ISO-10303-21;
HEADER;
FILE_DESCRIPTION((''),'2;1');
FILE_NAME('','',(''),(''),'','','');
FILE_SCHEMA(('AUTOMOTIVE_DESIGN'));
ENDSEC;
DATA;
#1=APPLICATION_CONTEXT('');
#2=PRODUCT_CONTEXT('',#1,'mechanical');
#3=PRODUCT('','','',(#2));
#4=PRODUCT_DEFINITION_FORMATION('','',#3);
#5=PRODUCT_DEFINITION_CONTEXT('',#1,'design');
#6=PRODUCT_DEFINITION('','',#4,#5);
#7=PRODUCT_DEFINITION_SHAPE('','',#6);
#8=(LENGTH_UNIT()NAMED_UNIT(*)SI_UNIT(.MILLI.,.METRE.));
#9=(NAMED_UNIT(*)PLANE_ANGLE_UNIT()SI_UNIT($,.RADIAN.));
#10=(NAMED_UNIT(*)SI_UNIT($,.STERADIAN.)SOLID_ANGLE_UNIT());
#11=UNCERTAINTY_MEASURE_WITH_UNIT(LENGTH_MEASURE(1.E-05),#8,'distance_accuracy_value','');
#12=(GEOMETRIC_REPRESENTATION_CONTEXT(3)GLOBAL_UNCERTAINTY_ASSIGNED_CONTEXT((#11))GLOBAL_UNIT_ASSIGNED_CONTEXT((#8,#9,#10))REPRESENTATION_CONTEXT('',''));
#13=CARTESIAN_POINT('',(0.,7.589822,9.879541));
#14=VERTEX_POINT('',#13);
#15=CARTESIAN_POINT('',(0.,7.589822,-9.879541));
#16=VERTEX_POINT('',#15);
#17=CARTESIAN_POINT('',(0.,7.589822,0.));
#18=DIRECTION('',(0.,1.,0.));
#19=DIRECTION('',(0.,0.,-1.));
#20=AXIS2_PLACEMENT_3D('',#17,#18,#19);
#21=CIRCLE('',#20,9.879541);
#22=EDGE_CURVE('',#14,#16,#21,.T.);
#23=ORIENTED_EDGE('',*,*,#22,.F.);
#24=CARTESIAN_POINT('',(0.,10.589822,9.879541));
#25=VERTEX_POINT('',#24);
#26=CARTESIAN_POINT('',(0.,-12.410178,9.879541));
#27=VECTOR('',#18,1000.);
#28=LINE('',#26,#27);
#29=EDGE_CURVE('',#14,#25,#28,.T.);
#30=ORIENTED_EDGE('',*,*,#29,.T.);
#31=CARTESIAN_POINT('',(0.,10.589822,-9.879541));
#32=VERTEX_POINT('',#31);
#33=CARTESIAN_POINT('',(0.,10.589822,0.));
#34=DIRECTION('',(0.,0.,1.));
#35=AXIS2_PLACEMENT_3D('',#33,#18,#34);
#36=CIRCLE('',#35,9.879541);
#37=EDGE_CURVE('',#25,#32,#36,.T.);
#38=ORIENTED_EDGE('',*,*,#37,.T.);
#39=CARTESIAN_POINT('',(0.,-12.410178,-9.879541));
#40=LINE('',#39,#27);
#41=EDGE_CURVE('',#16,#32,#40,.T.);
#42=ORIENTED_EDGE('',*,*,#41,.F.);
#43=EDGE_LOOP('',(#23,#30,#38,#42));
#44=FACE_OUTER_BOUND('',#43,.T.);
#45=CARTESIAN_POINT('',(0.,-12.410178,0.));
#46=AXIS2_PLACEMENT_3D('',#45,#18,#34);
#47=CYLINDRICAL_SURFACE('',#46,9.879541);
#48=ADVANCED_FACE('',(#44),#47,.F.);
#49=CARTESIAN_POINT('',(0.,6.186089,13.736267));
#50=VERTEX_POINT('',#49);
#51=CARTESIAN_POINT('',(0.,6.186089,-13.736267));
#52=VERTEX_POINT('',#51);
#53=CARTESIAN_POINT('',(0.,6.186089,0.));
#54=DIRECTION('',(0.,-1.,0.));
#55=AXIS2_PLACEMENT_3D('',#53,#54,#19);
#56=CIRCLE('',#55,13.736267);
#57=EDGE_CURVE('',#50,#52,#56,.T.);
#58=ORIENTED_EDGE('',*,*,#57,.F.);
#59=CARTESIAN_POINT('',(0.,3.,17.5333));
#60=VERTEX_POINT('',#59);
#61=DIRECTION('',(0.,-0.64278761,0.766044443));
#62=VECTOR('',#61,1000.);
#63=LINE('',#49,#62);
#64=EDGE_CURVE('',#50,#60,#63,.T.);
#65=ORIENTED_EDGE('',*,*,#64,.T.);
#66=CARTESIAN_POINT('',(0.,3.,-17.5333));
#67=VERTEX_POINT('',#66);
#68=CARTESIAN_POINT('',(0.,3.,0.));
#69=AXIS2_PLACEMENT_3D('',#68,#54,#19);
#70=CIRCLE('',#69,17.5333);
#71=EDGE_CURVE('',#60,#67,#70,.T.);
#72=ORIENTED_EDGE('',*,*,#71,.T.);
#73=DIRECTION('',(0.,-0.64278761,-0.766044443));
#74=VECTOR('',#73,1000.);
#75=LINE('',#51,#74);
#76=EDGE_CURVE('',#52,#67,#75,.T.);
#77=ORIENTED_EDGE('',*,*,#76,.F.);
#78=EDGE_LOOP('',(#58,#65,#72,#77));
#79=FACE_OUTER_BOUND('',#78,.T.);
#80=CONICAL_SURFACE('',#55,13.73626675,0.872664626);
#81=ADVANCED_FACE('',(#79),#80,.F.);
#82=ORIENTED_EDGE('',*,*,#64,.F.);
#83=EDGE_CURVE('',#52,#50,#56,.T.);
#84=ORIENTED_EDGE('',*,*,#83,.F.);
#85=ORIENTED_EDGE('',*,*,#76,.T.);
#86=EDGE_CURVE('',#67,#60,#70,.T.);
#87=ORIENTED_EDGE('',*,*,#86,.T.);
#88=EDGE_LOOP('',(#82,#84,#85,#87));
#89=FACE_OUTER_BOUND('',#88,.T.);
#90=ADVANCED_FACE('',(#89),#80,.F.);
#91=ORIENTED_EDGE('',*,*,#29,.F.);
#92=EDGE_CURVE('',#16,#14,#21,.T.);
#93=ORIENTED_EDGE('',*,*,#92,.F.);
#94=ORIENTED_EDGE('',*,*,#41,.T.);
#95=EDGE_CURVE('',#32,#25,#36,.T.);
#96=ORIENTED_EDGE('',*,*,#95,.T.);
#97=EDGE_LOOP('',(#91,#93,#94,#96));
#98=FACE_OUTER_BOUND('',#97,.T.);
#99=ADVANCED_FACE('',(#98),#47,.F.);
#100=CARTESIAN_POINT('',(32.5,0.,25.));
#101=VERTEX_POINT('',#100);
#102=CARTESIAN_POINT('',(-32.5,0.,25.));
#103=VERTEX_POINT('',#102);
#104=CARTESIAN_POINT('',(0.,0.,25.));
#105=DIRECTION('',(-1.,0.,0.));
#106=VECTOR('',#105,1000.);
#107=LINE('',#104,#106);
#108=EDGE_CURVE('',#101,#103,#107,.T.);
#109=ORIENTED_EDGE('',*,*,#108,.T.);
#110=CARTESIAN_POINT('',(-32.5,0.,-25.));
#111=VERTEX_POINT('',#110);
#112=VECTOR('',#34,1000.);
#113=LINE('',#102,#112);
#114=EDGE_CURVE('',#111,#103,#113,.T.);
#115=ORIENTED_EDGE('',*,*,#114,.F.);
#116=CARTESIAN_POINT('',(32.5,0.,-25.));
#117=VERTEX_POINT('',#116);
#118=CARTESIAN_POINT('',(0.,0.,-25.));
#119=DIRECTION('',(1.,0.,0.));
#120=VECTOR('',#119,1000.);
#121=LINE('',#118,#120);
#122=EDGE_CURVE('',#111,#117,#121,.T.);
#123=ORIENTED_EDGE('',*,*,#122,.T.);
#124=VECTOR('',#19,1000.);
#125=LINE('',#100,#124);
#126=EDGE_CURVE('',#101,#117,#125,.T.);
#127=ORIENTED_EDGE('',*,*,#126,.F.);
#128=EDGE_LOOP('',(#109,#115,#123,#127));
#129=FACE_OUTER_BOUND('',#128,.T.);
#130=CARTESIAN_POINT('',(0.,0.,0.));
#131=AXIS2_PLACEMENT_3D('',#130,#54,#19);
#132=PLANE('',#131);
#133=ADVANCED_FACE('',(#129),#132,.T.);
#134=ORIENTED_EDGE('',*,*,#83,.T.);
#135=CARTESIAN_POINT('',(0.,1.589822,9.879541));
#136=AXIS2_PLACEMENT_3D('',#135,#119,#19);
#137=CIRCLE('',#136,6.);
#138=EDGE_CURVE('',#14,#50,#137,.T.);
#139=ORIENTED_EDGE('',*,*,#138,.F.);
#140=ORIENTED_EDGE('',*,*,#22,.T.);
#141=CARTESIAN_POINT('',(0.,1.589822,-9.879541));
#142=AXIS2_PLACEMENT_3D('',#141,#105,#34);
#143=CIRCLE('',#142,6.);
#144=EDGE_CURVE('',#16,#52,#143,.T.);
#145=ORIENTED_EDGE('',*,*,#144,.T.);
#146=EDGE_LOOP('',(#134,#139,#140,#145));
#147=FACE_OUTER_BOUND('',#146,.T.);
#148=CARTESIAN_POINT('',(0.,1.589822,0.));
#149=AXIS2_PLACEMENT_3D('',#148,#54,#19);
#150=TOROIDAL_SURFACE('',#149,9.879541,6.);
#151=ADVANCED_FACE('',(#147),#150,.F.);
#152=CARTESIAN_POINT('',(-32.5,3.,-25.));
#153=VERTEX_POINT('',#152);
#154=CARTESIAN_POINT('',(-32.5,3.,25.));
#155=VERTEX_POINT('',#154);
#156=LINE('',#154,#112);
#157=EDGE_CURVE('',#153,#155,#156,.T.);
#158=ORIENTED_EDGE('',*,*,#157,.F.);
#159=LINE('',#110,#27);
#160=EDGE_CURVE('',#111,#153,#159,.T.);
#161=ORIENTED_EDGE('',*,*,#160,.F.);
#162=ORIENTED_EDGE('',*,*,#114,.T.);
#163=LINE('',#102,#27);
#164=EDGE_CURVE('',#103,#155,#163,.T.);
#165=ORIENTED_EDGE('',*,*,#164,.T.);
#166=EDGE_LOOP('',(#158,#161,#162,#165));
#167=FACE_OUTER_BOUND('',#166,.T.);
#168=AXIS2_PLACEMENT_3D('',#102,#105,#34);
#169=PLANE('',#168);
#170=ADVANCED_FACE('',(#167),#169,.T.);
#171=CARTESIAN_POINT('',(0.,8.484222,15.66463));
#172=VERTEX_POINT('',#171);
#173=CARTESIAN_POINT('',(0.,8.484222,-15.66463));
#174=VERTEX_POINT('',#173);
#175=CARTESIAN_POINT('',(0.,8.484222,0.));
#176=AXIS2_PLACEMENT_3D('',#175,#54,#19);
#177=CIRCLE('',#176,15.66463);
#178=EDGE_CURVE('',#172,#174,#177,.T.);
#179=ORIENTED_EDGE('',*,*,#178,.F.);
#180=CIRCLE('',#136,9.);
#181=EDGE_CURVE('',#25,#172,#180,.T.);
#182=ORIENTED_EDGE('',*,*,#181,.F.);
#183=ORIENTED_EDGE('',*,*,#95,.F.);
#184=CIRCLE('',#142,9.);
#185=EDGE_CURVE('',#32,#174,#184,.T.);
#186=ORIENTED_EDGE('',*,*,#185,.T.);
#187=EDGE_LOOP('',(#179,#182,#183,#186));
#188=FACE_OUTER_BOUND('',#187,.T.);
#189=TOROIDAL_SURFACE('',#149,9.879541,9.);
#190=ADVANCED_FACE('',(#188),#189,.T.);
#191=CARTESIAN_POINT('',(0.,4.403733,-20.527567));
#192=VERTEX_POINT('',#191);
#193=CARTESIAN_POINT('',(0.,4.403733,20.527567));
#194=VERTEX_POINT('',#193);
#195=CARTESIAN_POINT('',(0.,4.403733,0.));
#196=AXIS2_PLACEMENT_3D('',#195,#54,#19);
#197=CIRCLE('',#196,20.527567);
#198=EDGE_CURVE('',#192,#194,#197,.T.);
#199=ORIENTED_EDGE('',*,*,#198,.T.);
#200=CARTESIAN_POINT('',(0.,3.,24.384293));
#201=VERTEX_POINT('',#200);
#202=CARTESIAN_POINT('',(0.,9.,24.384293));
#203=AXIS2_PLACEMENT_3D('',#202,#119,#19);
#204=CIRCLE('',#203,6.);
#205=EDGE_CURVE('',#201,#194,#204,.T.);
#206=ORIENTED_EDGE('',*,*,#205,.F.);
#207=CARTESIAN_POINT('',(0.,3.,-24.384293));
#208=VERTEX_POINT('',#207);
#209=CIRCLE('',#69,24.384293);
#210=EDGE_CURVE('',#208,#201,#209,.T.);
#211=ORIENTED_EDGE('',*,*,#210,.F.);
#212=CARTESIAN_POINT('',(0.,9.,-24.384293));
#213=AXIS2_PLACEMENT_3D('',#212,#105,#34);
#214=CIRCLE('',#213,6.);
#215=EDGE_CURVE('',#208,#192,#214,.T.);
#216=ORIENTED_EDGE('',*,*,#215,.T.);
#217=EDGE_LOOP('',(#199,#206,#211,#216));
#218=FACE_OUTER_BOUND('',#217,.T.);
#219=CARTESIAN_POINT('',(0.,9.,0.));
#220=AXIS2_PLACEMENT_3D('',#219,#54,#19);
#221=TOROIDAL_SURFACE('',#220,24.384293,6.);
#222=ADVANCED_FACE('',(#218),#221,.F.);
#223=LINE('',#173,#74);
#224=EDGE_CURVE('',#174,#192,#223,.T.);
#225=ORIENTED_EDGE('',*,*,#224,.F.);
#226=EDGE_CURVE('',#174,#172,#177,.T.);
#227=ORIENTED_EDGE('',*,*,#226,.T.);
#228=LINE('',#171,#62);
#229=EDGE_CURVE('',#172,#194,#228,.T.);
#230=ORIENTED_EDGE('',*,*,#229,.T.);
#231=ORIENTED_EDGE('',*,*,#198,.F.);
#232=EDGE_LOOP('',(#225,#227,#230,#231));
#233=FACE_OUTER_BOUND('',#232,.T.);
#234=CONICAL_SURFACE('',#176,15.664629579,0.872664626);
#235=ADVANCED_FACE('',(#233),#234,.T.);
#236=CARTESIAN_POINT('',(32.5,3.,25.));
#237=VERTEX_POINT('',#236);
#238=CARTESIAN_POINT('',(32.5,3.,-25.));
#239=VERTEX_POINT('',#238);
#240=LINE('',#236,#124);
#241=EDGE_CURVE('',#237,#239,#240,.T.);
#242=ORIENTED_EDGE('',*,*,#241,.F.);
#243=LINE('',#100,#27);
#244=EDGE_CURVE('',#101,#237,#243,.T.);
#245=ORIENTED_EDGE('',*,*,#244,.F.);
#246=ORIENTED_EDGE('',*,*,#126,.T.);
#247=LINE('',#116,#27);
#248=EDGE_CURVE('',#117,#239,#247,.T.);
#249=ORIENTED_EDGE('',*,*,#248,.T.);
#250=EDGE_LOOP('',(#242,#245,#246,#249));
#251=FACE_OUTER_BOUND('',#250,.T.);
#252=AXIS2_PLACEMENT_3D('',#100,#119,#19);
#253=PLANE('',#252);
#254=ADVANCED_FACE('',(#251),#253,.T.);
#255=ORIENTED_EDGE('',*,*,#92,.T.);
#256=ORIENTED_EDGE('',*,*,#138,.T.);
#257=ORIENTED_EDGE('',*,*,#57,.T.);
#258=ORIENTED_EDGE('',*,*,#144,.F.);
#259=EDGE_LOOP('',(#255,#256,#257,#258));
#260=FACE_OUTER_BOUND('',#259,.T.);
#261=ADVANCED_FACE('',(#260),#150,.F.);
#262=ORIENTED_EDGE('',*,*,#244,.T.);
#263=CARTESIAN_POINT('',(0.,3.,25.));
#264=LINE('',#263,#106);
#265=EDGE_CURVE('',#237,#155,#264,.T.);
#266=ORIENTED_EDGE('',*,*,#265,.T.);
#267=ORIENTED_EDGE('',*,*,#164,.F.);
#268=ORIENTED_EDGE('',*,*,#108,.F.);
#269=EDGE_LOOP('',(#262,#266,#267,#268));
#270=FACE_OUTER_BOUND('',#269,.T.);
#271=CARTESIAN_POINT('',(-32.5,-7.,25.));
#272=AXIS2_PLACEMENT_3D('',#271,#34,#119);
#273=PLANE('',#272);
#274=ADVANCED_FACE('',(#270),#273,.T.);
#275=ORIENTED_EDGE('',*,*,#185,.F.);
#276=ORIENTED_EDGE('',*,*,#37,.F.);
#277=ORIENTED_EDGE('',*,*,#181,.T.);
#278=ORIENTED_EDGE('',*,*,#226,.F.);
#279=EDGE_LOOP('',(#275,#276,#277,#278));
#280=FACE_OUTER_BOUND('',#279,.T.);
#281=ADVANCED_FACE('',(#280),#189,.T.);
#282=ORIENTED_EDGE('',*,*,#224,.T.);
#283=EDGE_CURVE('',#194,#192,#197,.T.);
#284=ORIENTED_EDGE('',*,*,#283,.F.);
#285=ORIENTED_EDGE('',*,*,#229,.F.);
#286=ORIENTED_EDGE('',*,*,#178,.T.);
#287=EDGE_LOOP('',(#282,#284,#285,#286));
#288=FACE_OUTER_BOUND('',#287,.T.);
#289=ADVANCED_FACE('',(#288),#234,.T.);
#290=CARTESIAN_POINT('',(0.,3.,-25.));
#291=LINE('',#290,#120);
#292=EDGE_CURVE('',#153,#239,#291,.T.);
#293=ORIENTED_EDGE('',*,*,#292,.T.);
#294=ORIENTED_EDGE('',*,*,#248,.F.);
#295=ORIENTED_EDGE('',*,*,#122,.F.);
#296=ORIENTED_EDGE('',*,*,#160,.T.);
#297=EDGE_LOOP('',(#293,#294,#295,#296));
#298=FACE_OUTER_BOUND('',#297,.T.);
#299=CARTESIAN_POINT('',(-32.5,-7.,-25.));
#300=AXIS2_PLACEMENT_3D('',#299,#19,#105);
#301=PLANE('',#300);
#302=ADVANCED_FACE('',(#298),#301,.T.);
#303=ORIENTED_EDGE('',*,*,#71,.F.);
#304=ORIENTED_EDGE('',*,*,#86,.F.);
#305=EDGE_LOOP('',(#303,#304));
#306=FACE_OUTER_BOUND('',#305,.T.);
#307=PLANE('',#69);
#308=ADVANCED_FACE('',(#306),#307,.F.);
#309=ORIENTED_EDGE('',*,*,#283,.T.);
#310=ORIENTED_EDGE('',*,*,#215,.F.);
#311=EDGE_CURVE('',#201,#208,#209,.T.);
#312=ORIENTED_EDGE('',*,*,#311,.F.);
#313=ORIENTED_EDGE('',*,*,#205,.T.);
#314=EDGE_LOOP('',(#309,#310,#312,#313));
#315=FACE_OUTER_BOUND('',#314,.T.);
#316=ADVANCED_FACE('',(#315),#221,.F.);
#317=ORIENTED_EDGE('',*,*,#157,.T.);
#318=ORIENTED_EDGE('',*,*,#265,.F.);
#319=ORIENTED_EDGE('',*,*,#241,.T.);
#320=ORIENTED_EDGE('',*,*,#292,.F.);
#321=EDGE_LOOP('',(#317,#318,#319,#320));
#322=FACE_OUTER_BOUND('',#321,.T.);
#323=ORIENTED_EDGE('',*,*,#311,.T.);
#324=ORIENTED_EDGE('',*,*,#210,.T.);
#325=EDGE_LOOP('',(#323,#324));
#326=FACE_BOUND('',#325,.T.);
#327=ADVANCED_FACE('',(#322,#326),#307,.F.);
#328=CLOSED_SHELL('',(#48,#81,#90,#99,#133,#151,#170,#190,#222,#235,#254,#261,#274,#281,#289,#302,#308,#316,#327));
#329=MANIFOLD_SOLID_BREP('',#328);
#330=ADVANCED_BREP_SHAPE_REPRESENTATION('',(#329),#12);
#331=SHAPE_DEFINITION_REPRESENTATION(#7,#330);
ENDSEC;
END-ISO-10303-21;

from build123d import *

# Parameters (mm, degrees)
HUB_PROFILE_SKETCH_W                   = 7
HUB_PROFILE_SKETCH_H                   = 3
PLATE_OUTLINE_SKETCH_65X50_OUTSIDE_W   = 85.506
PLATE_OUTLINE_SKETCH_65X50_OUTSIDE_H   = 85.506
PLATE_OUTLINE_SKETCH_65X50_OUTSIDE_W_2 = 65
PLATE_OUTLINE_SKETCH_65X50_OUTSIDE_H_2 = 50
HUB_TRIM_CUT_65X50_DEPTH               = 10
BASE_PLATE_SKETCH_65X50_W              = 65
BASE_PLATE_SKETCH_65X50_H              = 50
BASE_PLATE_65X50X3_DEPTH               = 3
PLATE_CORNER_FILLETS_R6_R              = 6
MOUNTING_HOLES_SKETCH_R                = 2.5
MOUNTING_HOLES_4X_DEPTH                = 3
MOUNTING_HOLE_CHAMFERS_1_5X45_SIZE     = 1.5
CENTER_BORE_SKETCH_R                   = 9.879541092
CENTER_BORE_CUT_DEPTH                  = 23
HUB_GROOVE_SKETCH_45_R                 = 22.5
HUB_GROOVE_45_DEPTH                    = 3
SKETCH3_2_W                            = 65
SKETCH3_2_H                            = 50
PLATE_STEP_65X50X3_DEPTH               = 3


with BuildPart() as part:
    # Hub Profile Sketch → Hub Revolve (revolve)
    with BuildSketch(Plane.XY, mode=Mode.PRIVATE) as hub_revolve_sk:
        with Locations((3.5, 9.089822415)):
            Rectangle(HUB_PROFILE_SKETCH_W, HUB_PROFILE_SKETCH_H)
        with BuildLine():
            Line((9.879541092, 10.589822415), (7, 10.589822415))
            Line((7, 10.589822415), (7, 7.589822415))
            Line((7, 7.589822415), (9.879541092, 7.589822415))
            ThreePointArc((9.879541092, 7.589822415), (11.931661952, 7.22797814), (13.73626675, 6.186089074))
            Line((13.73626675, 6.186089074), (18.599204249, 2.105600012))
            ThreePointArc((18.599204249, 2.105600012), (21.306111446, 0.542766413), (24.384292736, 0))
            Line((24.384292736, 0), (32.5, 0))
            Line((32.5, 0), (32.5, 3))
            Line((32.5, 3), (24.384292736, 3))
            ThreePointArc((24.384292736, 3), (22.332171876, 3.361844275), (20.527567078, 4.403733341))
            Line((20.527567078, 4.403733341), (15.664629579, 8.484222403))
            ThreePointArc((15.664629579, 8.484222403), (12.957722382, 10.047056002), (9.879541092, 10.589822415))
        make_face()
    revolve(hub_revolve_sk.sketch.rotate(Axis((0, 0, 0), (0, 1, 0)), 90), axis=Axis((0, 0, 0), (0, 1, 0)))

    # Plate Outline Sketch 65x50 outside → Hub Trim Cut 65x50 (cut)
    with BuildSketch(Plane(origin=(0, 3, 0), x_dir=(1, 0, 0), z_dir=(0, 1, 0))):
        Rectangle(PLATE_OUTLINE_SKETCH_65X50_OUTSIDE_W, PLATE_OUTLINE_SKETCH_65X50_OUTSIDE_H)
        Rectangle(PLATE_OUTLINE_SKETCH_65X50_OUTSIDE_W_2, PLATE_OUTLINE_SKETCH_65X50_OUTSIDE_H_2, mode=Mode.SUBTRACT)
    extrude(amount=-HUB_TRIM_CUT_65X50_DEPTH, mode=Mode.SUBTRACT)

    # Base Plate Sketch 65x50 → Base Plate 65x50x3 (add)
    with BuildSketch(Plane(origin=(0, 3, 0), x_dir=(1, 0, 0), z_dir=(0, 1, 0))):
        Rectangle(BASE_PLATE_SKETCH_65X50_W, BASE_PLATE_SKETCH_65X50_H)
    extrude(amount=-BASE_PLATE_65X50X3_DEPTH)

    # Plate Corner Fillets R6
    plate_corner_fillets_r6_edges = [part.edges().sort_by_distance(p)[0] for p in [
        (32.5, 1.5, -25),
        (32.5, 1.5, 25),
        (-32.5, 1.5, 25),
        (-32.5, 1.5, -25),
    ]]
    fillet(plate_corner_fillets_r6_edges, radius=PLATE_CORNER_FILLETS_R6_R)

    # Mounting Holes Sketch → Mounting Holes 4x (cut)
    with BuildSketch(Plane(origin=(0, 3, 0), x_dir=(1, 0, 0), z_dir=(0, 1, 0))):
        with Locations(Location((-26.5, 19, 0), (0, 0, 270))):
            Circle(MOUNTING_HOLES_SKETCH_R)
        with Locations(Location((26.5, 19, 0), (0, 0, 270))):
            Circle(MOUNTING_HOLES_SKETCH_R)
        with Locations(Location((26.5, -19, 0), (0, 0, 270))):
            Circle(MOUNTING_HOLES_SKETCH_R)
        with Locations(Location((-26.5, -19, 0), (0, 0, 270))):
            Circle(MOUNTING_HOLES_SKETCH_R)
    extrude(amount=-MOUNTING_HOLES_4X_DEPTH, mode=Mode.SUBTRACT)

    # Mounting Hole Chamfers 1.5x45
    mounting_hole_chamfers_1_5x45_edges = [part.edges().sort_by_distance(p)[0] for p in [
        (-26.5, 3, 16.5),
        (26.5, 3, 16.5),
        (26.5, 3, -21.5),
        (-26.5, 3, -21.5),
    ]]
    chamfer(mounting_hole_chamfers_1_5x45_edges, length=MOUNTING_HOLE_CHAMFERS_1_5X45_SIZE)

    # Center Bore Sketch → Center Bore Cut (cut)
    with BuildSketch(Plane(origin=(0, 10.589822415, 0), x_dir=(1, 0, 0), z_dir=(0, 1, 0))):
        with Locations(Location((0, 0, 0), (0, 0, 90))):
            Circle(CENTER_BORE_SKETCH_R)
    extrude(amount=-CENTER_BORE_CUT_DEPTH, mode=Mode.SUBTRACT)

    # Hub Groove Sketch _45 → Hub Groove _45 (cut)
    with BuildSketch(Plane.XZ):
        with Locations(Location((0, 0, 0), (0, 0, 270))):
            Circle(HUB_GROOVE_SKETCH_45_R)
    extrude(amount=-HUB_GROOVE_45_DEPTH, mode=Mode.SUBTRACT)

    # Sketch3_2 → Plate Step 65x50x3 (add)
    with BuildSketch(Plane(origin=(0, 3, 0), x_dir=(1, 0, 0), z_dir=(0, 1, 0))):
        Rectangle(SKETCH3_2_W, SKETCH3_2_H)
    extrude(amount=-PLATE_STEP_65X50X3_DEPTH)


solid = part.part
